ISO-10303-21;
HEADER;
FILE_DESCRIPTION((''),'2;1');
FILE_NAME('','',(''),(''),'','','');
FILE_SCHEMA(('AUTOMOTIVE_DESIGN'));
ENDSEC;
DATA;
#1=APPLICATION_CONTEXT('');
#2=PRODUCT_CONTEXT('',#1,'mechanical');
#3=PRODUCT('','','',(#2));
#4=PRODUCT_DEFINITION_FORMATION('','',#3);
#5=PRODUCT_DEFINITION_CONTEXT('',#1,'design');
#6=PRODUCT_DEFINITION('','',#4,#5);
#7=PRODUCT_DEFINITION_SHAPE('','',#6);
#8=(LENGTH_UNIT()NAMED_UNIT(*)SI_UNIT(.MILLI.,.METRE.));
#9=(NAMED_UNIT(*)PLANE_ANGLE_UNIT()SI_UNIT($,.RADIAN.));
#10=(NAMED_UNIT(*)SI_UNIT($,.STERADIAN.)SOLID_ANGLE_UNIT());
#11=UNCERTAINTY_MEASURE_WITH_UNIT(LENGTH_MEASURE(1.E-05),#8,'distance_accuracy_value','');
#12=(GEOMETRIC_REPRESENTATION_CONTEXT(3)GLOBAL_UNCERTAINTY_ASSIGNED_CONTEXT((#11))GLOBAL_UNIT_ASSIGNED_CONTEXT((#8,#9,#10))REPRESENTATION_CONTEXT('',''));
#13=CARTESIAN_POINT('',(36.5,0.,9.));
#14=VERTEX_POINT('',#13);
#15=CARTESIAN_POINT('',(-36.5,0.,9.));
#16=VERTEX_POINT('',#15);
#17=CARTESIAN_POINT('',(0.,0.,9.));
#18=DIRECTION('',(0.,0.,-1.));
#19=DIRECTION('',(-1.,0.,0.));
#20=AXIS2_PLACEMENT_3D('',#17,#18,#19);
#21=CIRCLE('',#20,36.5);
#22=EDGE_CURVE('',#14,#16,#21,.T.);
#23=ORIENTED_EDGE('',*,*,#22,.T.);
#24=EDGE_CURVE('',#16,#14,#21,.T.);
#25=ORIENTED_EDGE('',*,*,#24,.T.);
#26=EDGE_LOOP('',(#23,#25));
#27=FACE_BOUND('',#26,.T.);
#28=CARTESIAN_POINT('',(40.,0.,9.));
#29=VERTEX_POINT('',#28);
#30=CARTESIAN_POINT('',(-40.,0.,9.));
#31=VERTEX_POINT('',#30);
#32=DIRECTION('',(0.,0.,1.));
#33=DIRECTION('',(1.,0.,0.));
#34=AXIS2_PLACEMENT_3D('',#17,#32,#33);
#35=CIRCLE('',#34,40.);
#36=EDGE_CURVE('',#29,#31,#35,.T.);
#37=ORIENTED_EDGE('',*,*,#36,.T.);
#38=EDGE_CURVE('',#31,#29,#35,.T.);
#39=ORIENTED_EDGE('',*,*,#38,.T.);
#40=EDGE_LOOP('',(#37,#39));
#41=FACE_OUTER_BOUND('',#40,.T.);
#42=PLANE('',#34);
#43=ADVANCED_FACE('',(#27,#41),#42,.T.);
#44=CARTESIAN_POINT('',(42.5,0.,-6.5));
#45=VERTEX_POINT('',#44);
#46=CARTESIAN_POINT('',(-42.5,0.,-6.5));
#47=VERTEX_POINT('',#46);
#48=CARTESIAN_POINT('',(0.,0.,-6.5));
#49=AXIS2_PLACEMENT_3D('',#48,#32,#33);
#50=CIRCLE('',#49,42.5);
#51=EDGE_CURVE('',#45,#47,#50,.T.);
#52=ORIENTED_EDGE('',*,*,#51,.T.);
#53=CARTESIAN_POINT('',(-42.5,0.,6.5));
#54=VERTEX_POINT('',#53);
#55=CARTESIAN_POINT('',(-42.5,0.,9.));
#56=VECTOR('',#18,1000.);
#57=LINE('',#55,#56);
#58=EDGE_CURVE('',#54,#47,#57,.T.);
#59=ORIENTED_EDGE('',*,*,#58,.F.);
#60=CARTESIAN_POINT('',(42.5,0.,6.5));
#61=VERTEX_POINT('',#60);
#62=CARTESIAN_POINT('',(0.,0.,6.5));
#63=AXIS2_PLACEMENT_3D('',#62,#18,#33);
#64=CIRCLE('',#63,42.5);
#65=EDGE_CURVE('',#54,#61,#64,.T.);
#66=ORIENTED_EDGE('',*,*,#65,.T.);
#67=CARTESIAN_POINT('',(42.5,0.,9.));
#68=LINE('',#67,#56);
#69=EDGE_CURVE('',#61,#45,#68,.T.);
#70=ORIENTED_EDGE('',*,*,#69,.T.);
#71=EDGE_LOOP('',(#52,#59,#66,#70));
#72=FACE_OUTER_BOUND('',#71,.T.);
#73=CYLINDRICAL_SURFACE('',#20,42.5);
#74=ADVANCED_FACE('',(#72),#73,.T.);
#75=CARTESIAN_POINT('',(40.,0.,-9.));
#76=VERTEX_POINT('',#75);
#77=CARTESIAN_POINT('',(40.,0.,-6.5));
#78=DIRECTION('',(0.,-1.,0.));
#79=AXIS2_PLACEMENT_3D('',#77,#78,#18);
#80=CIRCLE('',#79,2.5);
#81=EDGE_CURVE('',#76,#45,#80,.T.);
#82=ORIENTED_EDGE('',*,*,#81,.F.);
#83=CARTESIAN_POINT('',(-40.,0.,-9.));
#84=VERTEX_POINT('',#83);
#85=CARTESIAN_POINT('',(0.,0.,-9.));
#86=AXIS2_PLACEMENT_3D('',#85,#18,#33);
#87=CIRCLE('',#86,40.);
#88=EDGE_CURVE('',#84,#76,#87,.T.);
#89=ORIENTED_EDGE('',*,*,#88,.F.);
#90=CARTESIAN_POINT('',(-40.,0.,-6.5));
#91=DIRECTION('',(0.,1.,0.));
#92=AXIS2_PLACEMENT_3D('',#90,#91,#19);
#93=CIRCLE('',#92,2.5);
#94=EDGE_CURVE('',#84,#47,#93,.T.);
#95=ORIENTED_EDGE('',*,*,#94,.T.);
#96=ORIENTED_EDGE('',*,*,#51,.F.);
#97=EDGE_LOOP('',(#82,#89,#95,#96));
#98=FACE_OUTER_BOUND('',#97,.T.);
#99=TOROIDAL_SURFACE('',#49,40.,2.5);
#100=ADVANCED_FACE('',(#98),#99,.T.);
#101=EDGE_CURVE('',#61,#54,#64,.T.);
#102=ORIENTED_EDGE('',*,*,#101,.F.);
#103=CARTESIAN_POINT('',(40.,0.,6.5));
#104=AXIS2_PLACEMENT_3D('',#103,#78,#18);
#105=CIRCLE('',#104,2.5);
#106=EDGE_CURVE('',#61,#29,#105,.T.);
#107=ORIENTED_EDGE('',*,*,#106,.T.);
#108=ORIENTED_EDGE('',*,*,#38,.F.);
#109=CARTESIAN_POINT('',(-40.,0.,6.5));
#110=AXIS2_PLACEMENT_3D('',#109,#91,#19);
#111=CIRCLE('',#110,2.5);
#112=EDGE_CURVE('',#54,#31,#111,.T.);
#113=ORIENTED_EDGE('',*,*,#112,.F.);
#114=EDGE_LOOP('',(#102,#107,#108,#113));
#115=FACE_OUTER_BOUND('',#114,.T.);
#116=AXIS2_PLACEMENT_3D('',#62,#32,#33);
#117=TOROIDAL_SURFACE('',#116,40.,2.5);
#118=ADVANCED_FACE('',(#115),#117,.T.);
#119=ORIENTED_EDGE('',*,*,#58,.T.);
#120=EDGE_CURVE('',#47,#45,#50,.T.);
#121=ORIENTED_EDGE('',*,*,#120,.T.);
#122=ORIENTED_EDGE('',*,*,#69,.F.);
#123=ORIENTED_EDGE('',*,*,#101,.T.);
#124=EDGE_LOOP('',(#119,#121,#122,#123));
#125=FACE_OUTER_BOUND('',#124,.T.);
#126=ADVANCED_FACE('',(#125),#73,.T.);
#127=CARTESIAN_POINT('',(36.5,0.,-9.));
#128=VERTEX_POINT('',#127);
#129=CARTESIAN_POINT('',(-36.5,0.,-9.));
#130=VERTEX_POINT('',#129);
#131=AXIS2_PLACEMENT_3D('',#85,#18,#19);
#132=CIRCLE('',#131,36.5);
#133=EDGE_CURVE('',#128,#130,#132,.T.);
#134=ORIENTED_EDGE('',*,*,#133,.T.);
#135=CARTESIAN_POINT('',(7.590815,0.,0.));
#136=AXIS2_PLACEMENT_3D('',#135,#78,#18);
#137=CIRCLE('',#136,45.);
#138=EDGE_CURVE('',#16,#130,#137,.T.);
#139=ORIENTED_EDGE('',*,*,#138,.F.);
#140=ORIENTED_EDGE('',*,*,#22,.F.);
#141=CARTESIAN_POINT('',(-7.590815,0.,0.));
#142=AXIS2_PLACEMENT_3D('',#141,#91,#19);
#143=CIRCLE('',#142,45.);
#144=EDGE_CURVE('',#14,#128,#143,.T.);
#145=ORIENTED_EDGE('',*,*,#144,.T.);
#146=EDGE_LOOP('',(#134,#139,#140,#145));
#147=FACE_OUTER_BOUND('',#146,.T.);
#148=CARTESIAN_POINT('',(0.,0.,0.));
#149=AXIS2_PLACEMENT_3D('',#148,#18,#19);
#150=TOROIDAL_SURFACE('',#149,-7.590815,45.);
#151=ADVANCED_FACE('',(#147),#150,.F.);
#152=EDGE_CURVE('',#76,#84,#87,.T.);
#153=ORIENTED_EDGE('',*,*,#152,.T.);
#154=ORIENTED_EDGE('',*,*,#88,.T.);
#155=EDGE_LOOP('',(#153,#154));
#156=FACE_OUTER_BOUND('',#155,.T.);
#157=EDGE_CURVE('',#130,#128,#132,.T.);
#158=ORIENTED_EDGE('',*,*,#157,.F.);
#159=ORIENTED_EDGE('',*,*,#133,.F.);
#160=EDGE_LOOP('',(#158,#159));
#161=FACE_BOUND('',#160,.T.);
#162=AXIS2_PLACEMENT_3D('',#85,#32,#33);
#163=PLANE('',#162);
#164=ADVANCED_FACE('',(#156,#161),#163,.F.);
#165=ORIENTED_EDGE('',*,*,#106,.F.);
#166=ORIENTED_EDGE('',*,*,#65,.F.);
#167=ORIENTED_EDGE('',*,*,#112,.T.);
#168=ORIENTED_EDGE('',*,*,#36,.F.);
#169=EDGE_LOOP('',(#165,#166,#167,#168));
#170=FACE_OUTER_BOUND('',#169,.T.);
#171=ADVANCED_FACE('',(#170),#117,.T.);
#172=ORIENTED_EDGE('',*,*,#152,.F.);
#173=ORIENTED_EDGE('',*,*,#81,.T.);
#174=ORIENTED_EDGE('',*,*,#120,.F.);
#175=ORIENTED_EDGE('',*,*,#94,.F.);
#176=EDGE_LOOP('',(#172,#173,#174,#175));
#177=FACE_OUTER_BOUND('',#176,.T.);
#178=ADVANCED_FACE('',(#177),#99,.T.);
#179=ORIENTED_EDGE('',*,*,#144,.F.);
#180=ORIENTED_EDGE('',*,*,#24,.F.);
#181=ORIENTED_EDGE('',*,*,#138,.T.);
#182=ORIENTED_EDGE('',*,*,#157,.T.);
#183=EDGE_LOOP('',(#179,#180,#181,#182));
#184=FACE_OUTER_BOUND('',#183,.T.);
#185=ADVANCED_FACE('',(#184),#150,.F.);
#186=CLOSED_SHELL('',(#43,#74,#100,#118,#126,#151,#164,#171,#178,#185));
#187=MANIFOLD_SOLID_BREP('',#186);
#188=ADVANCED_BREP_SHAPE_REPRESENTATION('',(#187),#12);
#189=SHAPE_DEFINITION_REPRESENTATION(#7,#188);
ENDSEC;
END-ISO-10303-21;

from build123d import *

# Parameters (mm, degrees)
SKETCH1_R           = 42.5
SKETCH1_R_2         = 36.5
BOSS_EXTRUDE1_DEPTH = 9
FILLET1_R           = 2.5


with BuildPart() as part:
    # Sketch1 → Boss-Extrude1 (new, symmetric)
    with BuildSketch(Plane.XY):
        Circle(SKETCH1_R)
        Circle(SKETCH1_R_2, mode=Mode.SUBTRACT)
    extrude(amount=BOSS_EXTRUDE1_DEPTH, both=True)

    # Sketch2 → Cut-Revolve1 (revolve, cut)
    with BuildSketch(Plane(origin=(0, 0, 0), x_dir=(1, 0, 0), z_dir=(0, 1, 0)), mode=Mode.PRIVATE) as cut_revolve1_sk:
        with BuildLine():
            Line((36.5, 9), (36.5, -9))
            ThreePointArc((36.5, -9), (37.40918463, 0), (36.5, 9))
        make_face()
    revolve(cut_revolve1_sk.sketch.rotate(Axis((0, 0, 0), (0, 0, 1)), 180), axis=Axis((0, 0, 0), (0, 0, 1)), mode=Mode.SUBTRACT)

    # Fillet1
    fillet1_edges = [part.edges().sort_by_distance(p)[0] for p in [
        (-42.5, 0, -9),
        (-42.5, 0, 9),
    ]]
    fillet(fillet1_edges, radius=FILLET1_R)


solid = part.part
